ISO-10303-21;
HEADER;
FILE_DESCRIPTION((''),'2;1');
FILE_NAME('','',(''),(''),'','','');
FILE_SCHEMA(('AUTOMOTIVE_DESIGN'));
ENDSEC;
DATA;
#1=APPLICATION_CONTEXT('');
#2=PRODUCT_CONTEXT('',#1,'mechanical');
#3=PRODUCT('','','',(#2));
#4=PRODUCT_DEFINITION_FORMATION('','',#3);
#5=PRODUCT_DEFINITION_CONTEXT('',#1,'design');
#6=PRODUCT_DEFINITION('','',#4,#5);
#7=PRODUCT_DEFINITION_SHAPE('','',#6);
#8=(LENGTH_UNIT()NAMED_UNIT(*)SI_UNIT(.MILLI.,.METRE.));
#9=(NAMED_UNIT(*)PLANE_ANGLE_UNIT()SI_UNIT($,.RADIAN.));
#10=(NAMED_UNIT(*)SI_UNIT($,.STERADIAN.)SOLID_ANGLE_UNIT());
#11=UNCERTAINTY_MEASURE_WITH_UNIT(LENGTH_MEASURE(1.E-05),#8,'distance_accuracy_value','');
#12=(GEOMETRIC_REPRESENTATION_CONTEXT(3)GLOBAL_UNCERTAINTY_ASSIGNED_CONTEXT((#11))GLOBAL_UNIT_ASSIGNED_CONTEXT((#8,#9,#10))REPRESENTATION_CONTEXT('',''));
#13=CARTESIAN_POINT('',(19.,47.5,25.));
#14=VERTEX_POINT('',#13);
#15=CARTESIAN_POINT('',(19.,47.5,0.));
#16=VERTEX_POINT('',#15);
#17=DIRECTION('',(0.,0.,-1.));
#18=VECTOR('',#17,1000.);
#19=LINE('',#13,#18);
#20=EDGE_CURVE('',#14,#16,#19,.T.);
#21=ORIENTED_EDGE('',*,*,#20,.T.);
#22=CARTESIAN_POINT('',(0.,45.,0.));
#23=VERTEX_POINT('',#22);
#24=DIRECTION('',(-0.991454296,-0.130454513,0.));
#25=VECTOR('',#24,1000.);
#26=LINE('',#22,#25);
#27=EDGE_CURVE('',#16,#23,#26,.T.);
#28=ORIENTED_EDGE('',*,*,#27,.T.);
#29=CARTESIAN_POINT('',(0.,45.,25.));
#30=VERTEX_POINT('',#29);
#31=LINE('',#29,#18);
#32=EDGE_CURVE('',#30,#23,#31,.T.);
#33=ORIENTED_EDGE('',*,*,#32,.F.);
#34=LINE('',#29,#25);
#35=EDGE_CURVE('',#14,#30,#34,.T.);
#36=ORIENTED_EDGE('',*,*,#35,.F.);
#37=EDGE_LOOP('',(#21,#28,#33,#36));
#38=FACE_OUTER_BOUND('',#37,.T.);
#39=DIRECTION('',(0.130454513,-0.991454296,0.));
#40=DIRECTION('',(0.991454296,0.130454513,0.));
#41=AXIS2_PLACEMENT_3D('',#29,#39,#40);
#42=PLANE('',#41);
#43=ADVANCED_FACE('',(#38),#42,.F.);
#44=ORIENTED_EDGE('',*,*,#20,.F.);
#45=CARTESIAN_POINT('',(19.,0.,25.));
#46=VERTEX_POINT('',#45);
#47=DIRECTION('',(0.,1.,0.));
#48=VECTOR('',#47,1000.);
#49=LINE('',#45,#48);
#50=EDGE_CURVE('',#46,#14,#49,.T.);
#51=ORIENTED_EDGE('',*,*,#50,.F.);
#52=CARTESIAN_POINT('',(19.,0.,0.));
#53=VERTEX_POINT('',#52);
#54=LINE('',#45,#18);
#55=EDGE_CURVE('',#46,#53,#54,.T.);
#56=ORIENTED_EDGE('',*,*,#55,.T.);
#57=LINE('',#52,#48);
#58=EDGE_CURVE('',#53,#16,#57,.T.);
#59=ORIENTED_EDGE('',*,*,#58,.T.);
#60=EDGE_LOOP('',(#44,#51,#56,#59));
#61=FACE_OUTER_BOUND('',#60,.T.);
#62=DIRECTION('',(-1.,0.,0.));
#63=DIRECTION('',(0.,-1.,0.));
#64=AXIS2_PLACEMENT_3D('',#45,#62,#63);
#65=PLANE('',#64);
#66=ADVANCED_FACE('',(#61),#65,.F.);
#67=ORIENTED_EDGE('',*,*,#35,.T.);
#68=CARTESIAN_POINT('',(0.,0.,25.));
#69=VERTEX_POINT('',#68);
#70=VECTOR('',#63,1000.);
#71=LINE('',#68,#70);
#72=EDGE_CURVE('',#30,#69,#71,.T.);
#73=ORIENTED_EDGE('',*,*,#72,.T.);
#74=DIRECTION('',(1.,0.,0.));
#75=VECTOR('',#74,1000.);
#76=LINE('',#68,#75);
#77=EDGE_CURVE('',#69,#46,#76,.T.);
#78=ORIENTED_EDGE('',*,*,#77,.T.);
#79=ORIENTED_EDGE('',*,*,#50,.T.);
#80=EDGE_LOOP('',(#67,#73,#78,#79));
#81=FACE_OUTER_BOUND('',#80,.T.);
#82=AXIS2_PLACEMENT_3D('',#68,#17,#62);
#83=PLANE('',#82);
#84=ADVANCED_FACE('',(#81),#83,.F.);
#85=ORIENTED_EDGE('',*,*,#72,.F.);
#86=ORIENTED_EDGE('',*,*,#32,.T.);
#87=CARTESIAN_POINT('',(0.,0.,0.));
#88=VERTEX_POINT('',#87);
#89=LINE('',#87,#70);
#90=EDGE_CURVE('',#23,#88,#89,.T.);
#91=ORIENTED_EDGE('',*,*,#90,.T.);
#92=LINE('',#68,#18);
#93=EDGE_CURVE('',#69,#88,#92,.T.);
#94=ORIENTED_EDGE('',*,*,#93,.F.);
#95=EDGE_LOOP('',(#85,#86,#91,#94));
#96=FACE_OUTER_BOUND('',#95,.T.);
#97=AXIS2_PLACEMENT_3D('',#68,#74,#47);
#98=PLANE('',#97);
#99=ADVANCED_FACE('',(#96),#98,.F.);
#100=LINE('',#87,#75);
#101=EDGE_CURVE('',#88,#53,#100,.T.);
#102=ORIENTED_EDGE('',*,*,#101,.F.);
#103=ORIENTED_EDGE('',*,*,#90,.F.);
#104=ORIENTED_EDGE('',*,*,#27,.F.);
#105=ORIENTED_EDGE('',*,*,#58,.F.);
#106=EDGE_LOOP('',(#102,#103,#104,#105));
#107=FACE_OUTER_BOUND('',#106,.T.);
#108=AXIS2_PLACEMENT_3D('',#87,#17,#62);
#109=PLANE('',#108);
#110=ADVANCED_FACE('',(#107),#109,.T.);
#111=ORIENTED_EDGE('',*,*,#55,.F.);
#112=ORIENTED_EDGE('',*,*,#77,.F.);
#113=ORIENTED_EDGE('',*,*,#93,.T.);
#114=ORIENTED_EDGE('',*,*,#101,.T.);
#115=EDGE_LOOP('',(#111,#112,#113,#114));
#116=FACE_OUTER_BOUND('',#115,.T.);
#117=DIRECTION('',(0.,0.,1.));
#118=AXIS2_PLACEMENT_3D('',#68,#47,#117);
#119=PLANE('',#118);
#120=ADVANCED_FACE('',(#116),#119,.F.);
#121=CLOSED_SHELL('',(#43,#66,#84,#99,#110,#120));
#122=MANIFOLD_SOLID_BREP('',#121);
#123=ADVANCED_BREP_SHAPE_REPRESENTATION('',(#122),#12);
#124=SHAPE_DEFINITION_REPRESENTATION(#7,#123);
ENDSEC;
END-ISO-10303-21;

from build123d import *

# Parameters (mm, degrees)
BOSS_EXTRUDE1_DEPTH = 25


with BuildPart() as part:
    # Sketch1 → Boss-Extrude1 (new body)
    with BuildSketch(Plane.XY):
        Polygon((0, 45), (19, 47.5), (19, 0), (0, 0), align=None)
    extrude(amount=BOSS_EXTRUDE1_DEPTH)


solid = part.part
